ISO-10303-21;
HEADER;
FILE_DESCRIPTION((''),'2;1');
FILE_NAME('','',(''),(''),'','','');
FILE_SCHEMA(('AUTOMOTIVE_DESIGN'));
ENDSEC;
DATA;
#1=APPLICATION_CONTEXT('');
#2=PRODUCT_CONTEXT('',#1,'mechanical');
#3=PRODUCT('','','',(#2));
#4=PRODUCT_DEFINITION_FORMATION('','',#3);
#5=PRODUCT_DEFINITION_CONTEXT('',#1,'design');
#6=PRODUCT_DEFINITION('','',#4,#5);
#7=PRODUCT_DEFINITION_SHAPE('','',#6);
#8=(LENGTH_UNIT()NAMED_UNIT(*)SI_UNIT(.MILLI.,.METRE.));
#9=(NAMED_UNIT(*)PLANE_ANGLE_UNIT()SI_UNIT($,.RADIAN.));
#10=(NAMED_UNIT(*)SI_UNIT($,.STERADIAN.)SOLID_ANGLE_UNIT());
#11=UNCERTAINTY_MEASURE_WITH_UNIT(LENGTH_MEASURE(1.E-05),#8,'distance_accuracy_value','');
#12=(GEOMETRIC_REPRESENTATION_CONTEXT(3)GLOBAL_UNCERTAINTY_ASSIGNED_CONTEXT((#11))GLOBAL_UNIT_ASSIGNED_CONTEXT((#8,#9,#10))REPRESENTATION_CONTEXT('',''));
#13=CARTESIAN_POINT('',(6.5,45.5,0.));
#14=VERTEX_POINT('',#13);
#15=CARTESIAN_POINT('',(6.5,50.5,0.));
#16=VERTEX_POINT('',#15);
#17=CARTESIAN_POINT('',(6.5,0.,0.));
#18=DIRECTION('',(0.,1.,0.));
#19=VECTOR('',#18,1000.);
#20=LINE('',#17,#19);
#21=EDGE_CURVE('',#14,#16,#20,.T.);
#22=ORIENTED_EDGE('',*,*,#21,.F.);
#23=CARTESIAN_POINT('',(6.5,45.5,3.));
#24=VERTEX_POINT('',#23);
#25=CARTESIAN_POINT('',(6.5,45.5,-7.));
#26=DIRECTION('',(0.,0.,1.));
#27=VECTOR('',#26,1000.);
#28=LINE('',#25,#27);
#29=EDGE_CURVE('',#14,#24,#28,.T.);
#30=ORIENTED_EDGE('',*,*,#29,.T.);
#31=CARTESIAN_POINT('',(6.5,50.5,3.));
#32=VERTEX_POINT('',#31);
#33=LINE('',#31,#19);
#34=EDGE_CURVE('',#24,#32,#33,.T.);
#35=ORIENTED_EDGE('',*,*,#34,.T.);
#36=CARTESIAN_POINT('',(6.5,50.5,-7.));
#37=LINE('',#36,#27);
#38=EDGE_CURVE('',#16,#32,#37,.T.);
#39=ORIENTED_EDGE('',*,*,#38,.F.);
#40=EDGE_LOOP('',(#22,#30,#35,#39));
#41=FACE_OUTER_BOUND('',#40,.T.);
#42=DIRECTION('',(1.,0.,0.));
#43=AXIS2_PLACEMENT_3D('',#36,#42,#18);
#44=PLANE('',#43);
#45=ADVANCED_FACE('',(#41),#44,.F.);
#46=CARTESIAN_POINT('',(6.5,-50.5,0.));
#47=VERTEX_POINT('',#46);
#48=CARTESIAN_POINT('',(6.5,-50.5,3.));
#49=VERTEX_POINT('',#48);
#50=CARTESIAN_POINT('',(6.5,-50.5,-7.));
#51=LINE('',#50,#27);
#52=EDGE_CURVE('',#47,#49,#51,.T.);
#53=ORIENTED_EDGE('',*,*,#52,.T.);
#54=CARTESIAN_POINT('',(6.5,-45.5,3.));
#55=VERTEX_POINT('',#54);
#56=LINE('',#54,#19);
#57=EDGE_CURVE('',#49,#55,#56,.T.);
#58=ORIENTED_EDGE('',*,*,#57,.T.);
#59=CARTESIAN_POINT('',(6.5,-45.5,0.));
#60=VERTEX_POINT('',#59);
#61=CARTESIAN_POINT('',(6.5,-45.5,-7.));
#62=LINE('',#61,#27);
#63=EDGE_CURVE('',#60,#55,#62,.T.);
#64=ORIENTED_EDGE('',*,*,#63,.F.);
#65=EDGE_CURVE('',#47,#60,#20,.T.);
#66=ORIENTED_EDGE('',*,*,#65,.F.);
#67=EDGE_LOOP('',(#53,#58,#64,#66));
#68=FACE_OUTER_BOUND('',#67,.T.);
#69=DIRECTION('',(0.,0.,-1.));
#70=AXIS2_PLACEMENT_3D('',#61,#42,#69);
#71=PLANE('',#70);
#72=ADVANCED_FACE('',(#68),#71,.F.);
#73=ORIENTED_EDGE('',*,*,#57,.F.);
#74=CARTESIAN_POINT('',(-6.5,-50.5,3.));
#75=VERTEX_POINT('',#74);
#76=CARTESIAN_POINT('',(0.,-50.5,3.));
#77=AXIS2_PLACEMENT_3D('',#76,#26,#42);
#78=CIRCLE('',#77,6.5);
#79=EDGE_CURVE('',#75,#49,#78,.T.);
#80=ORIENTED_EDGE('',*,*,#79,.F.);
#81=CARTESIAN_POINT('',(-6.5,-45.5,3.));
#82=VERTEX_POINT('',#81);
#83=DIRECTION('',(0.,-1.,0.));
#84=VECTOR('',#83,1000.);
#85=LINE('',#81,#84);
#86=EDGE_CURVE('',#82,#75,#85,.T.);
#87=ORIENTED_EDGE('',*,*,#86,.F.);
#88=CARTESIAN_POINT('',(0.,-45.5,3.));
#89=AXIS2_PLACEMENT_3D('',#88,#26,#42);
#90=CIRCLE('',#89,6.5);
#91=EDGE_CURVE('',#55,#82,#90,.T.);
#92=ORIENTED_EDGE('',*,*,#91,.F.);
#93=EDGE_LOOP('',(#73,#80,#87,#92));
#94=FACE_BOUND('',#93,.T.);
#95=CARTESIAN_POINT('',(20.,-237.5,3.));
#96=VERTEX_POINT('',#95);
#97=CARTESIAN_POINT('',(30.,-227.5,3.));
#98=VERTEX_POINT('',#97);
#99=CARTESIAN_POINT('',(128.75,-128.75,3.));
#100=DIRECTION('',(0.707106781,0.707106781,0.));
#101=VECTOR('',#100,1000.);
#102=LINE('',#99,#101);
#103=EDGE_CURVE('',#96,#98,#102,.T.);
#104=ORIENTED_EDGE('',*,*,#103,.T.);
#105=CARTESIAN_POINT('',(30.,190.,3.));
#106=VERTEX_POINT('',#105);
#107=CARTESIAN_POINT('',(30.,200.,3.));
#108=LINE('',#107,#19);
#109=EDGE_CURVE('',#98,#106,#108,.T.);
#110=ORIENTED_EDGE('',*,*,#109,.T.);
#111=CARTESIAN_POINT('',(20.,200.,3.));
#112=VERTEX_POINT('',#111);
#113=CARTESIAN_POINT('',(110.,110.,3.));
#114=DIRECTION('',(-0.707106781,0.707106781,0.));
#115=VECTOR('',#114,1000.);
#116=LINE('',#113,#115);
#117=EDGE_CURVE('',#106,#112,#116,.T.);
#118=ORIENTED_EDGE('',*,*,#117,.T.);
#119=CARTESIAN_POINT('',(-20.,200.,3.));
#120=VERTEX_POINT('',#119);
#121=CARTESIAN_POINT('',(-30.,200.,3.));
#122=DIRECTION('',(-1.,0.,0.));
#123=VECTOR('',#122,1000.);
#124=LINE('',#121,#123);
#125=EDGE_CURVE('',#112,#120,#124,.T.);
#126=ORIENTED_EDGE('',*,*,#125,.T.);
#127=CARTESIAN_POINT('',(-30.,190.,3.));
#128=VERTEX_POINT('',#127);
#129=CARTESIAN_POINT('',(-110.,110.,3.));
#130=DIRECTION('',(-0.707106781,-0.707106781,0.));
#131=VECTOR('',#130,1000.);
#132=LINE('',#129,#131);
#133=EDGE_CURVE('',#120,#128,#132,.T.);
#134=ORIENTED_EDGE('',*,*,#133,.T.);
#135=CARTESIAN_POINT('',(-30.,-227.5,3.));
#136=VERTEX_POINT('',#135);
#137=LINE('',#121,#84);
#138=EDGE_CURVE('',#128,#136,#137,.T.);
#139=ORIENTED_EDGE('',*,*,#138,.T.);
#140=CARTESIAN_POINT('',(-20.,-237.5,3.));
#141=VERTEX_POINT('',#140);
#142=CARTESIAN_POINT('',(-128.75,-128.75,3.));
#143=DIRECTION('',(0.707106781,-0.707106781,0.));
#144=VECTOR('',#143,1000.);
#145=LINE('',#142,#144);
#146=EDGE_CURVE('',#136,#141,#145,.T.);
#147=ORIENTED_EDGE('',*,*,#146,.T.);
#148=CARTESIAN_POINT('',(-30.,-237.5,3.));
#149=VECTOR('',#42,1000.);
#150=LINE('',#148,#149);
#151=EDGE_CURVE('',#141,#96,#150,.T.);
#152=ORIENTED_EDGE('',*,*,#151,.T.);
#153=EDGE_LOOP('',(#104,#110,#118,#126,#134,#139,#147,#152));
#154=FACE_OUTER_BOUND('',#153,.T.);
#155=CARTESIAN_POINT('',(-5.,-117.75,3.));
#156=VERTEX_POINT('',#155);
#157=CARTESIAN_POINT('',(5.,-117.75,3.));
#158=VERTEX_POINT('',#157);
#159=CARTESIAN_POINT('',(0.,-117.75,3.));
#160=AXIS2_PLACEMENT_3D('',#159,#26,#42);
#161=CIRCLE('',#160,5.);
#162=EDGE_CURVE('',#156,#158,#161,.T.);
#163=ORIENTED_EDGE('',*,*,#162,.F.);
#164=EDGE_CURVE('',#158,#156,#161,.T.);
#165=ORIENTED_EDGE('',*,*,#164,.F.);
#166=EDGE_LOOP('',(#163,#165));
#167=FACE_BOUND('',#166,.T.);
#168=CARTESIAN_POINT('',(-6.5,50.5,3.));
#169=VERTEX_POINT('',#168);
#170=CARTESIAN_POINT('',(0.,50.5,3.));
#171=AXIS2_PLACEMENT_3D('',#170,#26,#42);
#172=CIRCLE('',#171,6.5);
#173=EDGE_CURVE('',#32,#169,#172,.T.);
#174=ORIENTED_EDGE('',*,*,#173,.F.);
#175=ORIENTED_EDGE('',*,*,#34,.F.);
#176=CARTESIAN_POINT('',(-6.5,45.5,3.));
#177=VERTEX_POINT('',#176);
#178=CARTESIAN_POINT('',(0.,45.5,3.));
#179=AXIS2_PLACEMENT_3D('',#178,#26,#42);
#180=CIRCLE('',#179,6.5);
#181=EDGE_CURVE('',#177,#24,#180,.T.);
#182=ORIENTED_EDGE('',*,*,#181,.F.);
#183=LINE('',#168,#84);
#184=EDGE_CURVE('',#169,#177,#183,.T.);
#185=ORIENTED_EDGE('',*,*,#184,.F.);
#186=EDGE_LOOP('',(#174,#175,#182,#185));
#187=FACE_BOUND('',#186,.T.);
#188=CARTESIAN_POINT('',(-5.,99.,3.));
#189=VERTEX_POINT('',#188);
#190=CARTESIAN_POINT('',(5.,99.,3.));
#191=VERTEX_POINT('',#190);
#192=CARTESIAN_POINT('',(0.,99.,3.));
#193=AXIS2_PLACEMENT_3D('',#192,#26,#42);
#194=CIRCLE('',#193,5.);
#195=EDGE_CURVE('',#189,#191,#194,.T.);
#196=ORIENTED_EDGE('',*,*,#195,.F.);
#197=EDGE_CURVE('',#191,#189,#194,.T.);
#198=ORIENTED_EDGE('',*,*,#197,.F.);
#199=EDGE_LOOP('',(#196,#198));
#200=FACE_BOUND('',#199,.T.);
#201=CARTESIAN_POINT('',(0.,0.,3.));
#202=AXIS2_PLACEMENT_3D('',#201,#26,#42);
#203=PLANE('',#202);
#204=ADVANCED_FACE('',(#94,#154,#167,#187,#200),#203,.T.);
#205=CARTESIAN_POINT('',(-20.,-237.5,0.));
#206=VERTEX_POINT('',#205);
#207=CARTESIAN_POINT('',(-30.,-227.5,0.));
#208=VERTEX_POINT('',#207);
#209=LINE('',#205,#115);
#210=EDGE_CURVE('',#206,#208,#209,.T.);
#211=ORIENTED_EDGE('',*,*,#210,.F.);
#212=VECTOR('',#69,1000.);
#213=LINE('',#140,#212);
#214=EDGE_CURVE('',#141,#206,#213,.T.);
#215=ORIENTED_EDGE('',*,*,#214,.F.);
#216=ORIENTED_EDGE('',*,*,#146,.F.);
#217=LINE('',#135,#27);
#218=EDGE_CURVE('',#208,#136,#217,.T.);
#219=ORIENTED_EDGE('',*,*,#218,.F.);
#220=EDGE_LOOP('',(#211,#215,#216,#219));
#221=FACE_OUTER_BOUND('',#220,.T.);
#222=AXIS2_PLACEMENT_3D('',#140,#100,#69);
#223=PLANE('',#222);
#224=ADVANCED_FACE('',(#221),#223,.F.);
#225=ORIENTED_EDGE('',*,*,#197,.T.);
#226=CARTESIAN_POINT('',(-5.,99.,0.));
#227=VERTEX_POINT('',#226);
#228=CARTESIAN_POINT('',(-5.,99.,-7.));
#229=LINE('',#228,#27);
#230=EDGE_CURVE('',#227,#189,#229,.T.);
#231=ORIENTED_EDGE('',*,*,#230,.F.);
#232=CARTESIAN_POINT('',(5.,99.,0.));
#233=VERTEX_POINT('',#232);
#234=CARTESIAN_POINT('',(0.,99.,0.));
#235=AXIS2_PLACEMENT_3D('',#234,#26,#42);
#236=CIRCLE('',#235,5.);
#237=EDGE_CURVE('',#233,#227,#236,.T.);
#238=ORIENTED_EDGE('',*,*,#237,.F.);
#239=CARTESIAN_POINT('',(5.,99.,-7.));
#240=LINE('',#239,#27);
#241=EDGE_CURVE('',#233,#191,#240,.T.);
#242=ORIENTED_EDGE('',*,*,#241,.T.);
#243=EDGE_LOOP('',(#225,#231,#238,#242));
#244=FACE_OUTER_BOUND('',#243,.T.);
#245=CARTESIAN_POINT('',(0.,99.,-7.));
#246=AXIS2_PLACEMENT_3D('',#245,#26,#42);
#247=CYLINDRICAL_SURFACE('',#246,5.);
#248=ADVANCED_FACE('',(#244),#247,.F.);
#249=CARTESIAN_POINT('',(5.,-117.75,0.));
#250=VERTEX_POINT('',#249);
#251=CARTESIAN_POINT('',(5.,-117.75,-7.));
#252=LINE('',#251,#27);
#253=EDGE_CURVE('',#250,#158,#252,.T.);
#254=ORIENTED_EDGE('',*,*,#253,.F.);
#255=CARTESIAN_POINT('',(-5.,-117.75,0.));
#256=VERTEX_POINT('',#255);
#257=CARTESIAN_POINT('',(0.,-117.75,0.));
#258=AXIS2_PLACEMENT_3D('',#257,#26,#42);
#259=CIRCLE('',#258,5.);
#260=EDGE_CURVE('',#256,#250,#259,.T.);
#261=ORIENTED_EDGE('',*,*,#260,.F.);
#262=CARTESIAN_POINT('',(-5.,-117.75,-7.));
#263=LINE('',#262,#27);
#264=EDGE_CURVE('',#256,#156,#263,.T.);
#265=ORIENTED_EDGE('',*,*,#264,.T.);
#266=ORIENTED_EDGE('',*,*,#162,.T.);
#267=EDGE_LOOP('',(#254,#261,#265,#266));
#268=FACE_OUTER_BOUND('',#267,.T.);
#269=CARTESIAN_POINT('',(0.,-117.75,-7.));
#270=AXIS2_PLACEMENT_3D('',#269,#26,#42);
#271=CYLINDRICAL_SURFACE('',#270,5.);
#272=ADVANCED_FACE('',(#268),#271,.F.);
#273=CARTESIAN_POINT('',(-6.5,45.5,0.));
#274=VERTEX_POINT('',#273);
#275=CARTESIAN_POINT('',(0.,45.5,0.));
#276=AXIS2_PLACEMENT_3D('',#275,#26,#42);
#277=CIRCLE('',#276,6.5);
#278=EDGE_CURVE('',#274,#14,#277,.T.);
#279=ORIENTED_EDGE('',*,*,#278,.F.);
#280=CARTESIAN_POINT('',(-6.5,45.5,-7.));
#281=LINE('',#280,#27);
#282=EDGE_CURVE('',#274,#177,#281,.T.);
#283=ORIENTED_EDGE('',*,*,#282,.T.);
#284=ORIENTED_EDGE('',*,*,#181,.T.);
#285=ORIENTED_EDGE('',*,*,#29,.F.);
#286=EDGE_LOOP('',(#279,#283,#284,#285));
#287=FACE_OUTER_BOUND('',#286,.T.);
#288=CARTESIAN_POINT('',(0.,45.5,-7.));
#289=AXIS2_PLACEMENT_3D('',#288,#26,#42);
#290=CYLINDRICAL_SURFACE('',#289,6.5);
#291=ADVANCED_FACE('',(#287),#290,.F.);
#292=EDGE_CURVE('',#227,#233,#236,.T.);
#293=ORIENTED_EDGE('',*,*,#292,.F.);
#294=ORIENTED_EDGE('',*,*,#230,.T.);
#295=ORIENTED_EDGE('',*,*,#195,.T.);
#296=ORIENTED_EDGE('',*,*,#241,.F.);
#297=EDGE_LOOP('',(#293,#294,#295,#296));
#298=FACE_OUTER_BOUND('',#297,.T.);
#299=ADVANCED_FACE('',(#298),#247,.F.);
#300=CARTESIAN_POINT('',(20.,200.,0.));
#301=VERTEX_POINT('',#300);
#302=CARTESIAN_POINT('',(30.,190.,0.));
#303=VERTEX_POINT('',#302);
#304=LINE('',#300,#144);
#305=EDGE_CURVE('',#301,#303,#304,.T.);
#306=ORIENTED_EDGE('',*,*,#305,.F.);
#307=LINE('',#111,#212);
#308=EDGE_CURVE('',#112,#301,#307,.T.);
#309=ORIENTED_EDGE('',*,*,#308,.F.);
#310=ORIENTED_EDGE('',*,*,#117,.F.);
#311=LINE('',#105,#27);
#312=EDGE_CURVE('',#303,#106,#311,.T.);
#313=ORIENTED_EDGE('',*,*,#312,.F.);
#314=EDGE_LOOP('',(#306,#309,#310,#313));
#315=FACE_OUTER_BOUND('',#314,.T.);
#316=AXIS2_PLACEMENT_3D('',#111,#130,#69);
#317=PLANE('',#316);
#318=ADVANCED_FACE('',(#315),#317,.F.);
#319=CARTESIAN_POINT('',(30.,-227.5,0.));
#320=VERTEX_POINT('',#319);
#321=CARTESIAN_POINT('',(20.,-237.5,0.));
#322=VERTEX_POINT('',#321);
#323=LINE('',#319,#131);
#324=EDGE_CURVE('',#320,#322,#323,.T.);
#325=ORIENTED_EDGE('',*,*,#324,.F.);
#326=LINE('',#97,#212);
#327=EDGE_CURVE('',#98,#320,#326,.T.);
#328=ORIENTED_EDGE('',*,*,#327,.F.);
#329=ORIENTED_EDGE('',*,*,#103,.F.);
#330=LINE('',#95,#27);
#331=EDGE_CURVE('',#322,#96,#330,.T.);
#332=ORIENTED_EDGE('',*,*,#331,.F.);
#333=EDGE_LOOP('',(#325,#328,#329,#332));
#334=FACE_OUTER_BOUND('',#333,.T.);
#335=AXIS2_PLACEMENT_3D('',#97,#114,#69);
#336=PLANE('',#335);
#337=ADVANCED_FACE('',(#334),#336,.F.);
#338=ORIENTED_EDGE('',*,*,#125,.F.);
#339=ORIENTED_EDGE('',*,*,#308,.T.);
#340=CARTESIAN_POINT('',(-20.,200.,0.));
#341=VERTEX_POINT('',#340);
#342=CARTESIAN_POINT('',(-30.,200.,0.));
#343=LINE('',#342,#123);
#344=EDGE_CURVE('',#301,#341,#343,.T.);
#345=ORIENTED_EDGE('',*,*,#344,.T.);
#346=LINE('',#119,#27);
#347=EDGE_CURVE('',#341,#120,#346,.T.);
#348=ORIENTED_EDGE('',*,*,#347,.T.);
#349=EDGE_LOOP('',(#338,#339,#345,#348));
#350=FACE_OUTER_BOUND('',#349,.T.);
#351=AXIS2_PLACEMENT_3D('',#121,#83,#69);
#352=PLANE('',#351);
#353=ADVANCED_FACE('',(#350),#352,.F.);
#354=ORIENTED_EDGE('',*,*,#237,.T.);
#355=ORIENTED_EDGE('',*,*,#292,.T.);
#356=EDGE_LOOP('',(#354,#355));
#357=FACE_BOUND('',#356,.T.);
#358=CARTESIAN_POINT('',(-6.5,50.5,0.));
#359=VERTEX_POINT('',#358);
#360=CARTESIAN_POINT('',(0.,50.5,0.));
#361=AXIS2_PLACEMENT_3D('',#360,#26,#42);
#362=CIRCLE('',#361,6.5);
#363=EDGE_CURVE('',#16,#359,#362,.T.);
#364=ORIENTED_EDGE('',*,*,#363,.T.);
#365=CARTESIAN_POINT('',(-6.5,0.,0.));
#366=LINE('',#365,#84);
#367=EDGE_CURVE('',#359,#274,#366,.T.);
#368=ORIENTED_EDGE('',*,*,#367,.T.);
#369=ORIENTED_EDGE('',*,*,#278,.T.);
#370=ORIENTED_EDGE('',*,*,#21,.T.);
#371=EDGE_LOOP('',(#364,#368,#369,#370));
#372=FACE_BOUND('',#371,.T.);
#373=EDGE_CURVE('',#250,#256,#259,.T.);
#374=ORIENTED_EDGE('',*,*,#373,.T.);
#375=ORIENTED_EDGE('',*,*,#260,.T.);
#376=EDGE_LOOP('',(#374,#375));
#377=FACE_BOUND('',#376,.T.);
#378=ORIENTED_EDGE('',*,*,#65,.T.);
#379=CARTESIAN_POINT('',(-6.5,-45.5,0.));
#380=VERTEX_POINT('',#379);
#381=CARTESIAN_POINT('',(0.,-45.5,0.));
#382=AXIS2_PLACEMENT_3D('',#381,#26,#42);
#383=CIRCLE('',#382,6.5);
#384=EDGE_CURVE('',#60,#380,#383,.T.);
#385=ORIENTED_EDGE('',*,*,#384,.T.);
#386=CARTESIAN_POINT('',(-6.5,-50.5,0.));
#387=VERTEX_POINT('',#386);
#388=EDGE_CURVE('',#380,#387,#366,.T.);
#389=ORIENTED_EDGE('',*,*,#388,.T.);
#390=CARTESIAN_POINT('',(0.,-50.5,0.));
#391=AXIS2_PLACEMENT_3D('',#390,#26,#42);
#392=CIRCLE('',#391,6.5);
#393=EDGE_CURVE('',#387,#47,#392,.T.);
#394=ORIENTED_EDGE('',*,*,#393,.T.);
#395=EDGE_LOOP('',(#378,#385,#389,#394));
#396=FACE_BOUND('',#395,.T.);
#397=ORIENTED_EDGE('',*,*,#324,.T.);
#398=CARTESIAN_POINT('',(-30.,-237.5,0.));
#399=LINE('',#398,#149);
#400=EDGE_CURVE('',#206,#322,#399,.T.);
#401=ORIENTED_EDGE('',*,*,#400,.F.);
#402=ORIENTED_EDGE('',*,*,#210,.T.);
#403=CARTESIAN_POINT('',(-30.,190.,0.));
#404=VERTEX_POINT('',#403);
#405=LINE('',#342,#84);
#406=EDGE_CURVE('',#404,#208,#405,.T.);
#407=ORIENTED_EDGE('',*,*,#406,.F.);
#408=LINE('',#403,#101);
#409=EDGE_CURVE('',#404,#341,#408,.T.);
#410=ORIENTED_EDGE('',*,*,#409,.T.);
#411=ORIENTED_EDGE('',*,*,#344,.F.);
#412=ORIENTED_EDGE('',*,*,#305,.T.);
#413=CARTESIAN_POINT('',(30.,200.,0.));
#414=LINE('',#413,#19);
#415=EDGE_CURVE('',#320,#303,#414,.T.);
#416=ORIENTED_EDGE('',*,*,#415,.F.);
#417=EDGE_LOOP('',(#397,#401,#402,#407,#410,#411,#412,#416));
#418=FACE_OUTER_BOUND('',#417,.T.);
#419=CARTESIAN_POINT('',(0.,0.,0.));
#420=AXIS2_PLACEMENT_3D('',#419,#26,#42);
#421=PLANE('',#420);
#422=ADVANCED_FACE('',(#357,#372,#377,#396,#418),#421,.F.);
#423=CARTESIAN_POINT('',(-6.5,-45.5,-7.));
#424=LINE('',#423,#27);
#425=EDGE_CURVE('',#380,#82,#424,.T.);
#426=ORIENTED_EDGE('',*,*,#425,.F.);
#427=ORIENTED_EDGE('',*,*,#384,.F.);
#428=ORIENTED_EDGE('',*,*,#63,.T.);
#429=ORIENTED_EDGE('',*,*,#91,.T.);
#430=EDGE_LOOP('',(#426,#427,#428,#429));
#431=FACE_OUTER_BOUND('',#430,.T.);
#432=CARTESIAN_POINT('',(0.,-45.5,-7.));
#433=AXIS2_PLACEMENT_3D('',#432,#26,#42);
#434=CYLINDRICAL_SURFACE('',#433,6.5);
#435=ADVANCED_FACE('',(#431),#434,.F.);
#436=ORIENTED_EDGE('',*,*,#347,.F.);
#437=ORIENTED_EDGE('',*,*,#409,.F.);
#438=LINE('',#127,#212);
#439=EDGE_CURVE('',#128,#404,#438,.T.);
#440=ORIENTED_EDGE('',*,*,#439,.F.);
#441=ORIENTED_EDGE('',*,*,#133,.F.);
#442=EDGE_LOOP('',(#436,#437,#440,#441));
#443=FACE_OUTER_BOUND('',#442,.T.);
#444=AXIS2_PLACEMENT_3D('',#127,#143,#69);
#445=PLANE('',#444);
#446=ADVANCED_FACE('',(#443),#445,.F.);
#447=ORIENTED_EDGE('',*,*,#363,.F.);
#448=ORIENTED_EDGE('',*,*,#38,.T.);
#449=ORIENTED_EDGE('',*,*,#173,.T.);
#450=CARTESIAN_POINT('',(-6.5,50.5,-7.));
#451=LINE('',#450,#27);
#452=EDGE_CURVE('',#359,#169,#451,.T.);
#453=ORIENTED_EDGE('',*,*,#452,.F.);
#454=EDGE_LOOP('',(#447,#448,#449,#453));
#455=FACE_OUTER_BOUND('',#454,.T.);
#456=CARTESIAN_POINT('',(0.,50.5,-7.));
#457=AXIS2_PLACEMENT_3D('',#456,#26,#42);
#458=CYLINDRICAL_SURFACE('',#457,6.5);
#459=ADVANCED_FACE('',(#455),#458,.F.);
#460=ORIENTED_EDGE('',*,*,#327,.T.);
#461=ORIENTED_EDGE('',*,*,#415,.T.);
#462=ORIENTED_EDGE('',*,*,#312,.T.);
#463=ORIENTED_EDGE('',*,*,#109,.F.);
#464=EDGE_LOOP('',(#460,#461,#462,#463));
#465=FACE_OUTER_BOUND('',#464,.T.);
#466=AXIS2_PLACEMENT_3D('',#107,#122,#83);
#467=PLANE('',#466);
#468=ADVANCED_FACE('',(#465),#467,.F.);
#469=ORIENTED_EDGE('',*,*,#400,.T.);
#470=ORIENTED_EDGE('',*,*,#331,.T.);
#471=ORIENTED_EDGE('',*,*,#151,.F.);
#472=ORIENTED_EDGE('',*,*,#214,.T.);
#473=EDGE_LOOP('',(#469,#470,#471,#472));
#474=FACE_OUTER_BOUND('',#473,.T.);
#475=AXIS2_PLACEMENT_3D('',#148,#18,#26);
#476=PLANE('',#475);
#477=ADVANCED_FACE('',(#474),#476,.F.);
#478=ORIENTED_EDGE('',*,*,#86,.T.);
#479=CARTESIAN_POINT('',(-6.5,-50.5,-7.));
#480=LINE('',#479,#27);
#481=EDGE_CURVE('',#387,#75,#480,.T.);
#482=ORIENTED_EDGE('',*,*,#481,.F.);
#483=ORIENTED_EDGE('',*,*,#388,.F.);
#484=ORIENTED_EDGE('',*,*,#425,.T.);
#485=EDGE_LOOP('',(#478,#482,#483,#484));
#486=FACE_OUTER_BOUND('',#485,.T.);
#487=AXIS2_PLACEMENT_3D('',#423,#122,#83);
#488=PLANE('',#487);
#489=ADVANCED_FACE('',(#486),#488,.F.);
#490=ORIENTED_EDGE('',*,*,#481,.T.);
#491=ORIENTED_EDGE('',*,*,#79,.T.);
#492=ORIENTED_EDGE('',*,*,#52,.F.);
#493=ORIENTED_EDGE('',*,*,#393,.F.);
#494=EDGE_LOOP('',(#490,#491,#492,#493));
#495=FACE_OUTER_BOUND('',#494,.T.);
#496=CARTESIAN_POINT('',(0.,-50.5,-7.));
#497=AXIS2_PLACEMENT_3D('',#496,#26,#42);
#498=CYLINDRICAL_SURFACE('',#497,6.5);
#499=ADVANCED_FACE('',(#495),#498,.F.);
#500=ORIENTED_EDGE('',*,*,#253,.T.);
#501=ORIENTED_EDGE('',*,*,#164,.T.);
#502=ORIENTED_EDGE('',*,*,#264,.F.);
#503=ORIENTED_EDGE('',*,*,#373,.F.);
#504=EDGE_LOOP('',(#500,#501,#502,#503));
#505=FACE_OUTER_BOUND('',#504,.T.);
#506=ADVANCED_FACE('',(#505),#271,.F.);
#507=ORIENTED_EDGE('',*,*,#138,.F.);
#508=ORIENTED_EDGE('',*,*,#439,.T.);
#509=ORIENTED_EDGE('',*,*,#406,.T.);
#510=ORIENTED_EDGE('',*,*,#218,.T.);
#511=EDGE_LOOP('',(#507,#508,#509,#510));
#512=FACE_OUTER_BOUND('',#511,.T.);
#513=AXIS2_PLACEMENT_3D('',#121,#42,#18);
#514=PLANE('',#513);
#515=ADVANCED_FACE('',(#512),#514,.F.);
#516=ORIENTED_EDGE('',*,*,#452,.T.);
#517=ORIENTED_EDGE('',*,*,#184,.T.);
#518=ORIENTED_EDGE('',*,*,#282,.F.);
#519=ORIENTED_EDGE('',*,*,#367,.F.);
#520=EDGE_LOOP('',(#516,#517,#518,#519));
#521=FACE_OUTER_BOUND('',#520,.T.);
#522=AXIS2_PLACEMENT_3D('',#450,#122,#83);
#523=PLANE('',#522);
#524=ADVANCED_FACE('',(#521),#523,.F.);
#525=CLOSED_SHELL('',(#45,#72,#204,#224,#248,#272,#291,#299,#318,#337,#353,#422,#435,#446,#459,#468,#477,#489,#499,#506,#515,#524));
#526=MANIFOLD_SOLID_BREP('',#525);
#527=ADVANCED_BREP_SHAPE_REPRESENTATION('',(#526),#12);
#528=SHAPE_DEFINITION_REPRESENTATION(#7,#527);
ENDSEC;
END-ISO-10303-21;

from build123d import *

# Parameters (mm, degrees)
SKETCH_1_W          = 60
SKETCH_1_H          = 437.5
EXTRUDE_1_DEPTH     = 3
CHAMFER_1_SIZE      = 10
SKETCH_2_R          = 5
CUT_EXTRUDE_1_DEPTH = 10


with BuildPart() as part:
    # 草图1 → 凸台-拉伸1 (new body)
    with BuildSketch(Plane.XY):
        with Locations((0, -18.75)):
            Rectangle(SKETCH_1_W, SKETCH_1_H)
    extrude(amount=EXTRUDE_1_DEPTH)

    # 倒角1
    chamfer_1_edges = [part.edges().sort_by_distance(p)[0] for p in [
        (30, -237.5, 1.5),
        (-30, -237.5, 1.5),
        (-30, 200, 1.5),
        (30, 200, 1.5),
    ]]
    chamfer(chamfer_1_edges, length=CHAMFER_1_SIZE)

    # 草图2 → 切除-拉伸1 (cut)
    with BuildSketch(Plane.XY.offset(3)):
        with Locations((0, 99)):
            Circle(SKETCH_2_R)
        with Locations((0, -117.75)):
            Circle(SKETCH_2_R)
        with BuildLine():
            Line((6.5, 50.5), (6.5, 45.5))
            ThreePointArc((6.5, 45.5), (0, 39), (-6.5, 45.5))
            Line((-6.5, 45.5), (-6.5, 50.5))
            ThreePointArc((-6.5, 50.5), (0, 57), (6.5, 50.5))
        make_face()
        with BuildLine():
            Line((6.5, -45.5), (6.5, -50.5))
            ThreePointArc((6.5, -50.5), (0, -57), (-6.5, -50.5))
            Line((-6.5, -50.5), (-6.5, -45.5))
            ThreePointArc((-6.5, -45.5), (0, -39), (6.5, -45.5))
        make_face()
    extrude(amount=-CUT_EXTRUDE_1_DEPTH, mode=Mode.SUBTRACT)


solid = part.part
